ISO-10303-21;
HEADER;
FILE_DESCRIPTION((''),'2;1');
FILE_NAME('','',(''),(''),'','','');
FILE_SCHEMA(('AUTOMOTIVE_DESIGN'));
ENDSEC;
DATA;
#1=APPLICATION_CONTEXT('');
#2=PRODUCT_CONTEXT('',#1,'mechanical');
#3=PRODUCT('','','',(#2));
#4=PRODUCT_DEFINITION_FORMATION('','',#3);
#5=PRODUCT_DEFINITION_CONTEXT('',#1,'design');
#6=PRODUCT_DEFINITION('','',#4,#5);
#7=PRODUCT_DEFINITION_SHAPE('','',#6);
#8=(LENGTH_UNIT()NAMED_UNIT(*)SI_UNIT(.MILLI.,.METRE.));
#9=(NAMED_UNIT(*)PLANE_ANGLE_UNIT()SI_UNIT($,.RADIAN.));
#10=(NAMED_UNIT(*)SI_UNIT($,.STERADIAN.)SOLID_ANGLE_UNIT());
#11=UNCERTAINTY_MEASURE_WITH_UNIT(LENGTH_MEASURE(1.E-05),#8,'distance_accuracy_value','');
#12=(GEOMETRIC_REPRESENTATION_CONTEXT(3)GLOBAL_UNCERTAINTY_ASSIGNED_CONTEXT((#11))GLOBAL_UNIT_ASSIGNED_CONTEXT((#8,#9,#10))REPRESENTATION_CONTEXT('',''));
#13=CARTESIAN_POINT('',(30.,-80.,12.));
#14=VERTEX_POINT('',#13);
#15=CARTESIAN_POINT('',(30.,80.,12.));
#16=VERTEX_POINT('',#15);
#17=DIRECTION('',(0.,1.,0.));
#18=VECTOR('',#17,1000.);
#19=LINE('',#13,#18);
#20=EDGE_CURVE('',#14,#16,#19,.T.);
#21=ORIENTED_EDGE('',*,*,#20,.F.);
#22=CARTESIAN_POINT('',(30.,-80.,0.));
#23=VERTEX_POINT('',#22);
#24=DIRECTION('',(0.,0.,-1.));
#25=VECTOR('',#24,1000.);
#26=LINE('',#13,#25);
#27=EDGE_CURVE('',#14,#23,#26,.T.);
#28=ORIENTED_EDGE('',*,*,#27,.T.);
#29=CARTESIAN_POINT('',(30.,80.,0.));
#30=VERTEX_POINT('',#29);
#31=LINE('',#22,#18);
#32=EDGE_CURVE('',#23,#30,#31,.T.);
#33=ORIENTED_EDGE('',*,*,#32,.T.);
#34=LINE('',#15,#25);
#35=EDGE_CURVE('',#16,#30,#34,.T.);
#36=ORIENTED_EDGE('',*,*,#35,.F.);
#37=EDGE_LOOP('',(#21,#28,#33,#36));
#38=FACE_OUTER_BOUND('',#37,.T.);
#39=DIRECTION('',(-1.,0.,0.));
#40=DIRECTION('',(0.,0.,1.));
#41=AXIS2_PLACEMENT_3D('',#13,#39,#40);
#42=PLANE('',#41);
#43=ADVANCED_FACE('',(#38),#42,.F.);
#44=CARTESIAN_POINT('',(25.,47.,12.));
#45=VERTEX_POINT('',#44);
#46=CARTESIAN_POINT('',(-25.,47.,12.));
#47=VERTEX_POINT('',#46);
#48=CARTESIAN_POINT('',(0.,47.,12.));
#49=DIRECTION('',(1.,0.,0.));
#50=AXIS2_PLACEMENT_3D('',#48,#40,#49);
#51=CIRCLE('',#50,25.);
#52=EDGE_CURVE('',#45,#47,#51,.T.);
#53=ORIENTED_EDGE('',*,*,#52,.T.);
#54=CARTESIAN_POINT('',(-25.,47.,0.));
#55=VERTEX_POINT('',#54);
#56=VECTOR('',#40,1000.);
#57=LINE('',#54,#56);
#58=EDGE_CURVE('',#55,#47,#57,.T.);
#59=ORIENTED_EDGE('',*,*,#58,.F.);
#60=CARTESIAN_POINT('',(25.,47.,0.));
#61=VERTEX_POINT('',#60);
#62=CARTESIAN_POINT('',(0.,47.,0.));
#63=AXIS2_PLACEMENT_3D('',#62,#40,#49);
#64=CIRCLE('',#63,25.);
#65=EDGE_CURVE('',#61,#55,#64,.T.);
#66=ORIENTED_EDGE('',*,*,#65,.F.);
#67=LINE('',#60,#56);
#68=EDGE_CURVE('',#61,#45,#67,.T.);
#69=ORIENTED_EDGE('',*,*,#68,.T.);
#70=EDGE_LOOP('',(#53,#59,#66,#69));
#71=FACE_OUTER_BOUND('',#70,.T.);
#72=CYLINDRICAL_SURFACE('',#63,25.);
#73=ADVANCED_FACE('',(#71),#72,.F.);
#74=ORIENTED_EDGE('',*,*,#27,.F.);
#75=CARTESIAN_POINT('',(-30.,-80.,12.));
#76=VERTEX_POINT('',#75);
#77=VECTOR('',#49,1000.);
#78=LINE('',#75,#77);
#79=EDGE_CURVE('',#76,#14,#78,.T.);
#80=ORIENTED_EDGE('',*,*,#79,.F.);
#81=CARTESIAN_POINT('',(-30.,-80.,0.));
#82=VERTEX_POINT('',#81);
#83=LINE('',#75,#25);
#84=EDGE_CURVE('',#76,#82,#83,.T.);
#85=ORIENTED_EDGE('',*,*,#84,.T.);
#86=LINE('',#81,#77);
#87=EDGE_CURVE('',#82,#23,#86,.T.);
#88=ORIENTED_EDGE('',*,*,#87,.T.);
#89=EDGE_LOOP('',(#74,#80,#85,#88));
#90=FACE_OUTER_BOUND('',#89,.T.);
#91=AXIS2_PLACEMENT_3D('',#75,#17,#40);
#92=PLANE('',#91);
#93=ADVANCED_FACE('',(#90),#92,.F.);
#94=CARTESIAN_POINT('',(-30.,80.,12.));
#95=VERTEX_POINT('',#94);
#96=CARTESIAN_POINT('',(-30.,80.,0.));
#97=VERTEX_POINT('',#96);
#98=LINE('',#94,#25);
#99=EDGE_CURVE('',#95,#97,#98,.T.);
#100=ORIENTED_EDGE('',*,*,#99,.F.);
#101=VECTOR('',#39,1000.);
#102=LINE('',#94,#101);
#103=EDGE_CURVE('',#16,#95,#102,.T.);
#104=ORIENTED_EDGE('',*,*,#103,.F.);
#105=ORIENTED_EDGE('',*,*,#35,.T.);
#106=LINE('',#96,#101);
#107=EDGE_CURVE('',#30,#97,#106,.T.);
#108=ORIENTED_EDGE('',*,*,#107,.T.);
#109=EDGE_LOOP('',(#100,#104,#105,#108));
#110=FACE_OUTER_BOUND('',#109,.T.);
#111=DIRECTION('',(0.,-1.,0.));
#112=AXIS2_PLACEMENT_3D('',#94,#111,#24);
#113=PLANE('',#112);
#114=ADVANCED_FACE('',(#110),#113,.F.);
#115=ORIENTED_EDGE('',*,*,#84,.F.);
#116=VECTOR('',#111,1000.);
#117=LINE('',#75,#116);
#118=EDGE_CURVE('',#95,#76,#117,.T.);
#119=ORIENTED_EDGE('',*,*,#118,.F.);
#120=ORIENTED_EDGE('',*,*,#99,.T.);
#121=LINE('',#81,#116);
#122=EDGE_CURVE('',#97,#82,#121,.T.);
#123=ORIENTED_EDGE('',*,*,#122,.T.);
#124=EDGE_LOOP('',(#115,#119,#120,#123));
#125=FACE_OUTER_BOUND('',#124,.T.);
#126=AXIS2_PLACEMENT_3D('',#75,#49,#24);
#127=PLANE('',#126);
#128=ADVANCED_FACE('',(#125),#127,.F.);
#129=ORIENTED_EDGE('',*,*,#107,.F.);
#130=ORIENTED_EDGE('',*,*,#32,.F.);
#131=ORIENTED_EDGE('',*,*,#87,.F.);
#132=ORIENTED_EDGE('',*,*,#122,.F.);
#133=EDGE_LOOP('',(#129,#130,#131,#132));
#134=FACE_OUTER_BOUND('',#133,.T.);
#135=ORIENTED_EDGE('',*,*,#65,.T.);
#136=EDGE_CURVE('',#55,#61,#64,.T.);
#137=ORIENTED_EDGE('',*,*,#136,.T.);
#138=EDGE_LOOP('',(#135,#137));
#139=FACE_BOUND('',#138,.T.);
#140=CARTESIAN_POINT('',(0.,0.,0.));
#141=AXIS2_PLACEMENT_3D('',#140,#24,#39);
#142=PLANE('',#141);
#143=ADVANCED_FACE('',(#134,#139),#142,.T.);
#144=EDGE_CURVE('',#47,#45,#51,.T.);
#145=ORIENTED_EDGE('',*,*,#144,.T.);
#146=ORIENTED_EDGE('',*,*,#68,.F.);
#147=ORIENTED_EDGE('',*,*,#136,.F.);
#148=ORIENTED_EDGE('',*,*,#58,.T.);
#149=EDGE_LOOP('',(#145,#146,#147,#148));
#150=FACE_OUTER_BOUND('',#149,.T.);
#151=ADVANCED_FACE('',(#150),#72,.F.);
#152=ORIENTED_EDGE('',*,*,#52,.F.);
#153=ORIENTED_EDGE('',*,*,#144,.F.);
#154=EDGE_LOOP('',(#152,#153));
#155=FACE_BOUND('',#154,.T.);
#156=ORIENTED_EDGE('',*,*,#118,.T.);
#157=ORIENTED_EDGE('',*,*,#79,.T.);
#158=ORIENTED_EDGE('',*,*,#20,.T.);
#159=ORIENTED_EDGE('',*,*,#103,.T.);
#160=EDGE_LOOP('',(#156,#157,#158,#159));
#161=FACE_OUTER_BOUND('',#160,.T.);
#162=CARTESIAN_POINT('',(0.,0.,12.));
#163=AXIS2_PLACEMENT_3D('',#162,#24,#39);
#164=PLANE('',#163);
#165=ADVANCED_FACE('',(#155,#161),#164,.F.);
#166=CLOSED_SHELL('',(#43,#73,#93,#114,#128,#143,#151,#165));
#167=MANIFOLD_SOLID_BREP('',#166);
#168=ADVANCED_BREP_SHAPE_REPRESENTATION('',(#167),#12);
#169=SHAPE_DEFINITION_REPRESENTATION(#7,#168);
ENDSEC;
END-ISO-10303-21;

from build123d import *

# Parameters (mm, degrees)
SKETCH_1_W          = 60
SKETCH_1_H          = 160
EXTRUDE_1_DEPTH     = 12
SKETCH_2_R          = 25
CUT_EXTRUDE_1_DEPTH = 87.27861844


with BuildPart() as part:
    # 草图1 → 凸台-拉伸1 (new body)
    with BuildSketch(Plane.XY):
        Rectangle(SKETCH_1_W, SKETCH_1_H)
    extrude(amount=EXTRUDE_1_DEPTH)

    # 草图2 → 切除-拉伸1 (cut, through all)
    with BuildSketch(Plane.XY.offset(12)):
        with Locations((0, 47)):
            Circle(SKETCH_2_R)
    extrude(amount=-CUT_EXTRUDE_1_DEPTH, mode=Mode.SUBTRACT)


solid = part.part
